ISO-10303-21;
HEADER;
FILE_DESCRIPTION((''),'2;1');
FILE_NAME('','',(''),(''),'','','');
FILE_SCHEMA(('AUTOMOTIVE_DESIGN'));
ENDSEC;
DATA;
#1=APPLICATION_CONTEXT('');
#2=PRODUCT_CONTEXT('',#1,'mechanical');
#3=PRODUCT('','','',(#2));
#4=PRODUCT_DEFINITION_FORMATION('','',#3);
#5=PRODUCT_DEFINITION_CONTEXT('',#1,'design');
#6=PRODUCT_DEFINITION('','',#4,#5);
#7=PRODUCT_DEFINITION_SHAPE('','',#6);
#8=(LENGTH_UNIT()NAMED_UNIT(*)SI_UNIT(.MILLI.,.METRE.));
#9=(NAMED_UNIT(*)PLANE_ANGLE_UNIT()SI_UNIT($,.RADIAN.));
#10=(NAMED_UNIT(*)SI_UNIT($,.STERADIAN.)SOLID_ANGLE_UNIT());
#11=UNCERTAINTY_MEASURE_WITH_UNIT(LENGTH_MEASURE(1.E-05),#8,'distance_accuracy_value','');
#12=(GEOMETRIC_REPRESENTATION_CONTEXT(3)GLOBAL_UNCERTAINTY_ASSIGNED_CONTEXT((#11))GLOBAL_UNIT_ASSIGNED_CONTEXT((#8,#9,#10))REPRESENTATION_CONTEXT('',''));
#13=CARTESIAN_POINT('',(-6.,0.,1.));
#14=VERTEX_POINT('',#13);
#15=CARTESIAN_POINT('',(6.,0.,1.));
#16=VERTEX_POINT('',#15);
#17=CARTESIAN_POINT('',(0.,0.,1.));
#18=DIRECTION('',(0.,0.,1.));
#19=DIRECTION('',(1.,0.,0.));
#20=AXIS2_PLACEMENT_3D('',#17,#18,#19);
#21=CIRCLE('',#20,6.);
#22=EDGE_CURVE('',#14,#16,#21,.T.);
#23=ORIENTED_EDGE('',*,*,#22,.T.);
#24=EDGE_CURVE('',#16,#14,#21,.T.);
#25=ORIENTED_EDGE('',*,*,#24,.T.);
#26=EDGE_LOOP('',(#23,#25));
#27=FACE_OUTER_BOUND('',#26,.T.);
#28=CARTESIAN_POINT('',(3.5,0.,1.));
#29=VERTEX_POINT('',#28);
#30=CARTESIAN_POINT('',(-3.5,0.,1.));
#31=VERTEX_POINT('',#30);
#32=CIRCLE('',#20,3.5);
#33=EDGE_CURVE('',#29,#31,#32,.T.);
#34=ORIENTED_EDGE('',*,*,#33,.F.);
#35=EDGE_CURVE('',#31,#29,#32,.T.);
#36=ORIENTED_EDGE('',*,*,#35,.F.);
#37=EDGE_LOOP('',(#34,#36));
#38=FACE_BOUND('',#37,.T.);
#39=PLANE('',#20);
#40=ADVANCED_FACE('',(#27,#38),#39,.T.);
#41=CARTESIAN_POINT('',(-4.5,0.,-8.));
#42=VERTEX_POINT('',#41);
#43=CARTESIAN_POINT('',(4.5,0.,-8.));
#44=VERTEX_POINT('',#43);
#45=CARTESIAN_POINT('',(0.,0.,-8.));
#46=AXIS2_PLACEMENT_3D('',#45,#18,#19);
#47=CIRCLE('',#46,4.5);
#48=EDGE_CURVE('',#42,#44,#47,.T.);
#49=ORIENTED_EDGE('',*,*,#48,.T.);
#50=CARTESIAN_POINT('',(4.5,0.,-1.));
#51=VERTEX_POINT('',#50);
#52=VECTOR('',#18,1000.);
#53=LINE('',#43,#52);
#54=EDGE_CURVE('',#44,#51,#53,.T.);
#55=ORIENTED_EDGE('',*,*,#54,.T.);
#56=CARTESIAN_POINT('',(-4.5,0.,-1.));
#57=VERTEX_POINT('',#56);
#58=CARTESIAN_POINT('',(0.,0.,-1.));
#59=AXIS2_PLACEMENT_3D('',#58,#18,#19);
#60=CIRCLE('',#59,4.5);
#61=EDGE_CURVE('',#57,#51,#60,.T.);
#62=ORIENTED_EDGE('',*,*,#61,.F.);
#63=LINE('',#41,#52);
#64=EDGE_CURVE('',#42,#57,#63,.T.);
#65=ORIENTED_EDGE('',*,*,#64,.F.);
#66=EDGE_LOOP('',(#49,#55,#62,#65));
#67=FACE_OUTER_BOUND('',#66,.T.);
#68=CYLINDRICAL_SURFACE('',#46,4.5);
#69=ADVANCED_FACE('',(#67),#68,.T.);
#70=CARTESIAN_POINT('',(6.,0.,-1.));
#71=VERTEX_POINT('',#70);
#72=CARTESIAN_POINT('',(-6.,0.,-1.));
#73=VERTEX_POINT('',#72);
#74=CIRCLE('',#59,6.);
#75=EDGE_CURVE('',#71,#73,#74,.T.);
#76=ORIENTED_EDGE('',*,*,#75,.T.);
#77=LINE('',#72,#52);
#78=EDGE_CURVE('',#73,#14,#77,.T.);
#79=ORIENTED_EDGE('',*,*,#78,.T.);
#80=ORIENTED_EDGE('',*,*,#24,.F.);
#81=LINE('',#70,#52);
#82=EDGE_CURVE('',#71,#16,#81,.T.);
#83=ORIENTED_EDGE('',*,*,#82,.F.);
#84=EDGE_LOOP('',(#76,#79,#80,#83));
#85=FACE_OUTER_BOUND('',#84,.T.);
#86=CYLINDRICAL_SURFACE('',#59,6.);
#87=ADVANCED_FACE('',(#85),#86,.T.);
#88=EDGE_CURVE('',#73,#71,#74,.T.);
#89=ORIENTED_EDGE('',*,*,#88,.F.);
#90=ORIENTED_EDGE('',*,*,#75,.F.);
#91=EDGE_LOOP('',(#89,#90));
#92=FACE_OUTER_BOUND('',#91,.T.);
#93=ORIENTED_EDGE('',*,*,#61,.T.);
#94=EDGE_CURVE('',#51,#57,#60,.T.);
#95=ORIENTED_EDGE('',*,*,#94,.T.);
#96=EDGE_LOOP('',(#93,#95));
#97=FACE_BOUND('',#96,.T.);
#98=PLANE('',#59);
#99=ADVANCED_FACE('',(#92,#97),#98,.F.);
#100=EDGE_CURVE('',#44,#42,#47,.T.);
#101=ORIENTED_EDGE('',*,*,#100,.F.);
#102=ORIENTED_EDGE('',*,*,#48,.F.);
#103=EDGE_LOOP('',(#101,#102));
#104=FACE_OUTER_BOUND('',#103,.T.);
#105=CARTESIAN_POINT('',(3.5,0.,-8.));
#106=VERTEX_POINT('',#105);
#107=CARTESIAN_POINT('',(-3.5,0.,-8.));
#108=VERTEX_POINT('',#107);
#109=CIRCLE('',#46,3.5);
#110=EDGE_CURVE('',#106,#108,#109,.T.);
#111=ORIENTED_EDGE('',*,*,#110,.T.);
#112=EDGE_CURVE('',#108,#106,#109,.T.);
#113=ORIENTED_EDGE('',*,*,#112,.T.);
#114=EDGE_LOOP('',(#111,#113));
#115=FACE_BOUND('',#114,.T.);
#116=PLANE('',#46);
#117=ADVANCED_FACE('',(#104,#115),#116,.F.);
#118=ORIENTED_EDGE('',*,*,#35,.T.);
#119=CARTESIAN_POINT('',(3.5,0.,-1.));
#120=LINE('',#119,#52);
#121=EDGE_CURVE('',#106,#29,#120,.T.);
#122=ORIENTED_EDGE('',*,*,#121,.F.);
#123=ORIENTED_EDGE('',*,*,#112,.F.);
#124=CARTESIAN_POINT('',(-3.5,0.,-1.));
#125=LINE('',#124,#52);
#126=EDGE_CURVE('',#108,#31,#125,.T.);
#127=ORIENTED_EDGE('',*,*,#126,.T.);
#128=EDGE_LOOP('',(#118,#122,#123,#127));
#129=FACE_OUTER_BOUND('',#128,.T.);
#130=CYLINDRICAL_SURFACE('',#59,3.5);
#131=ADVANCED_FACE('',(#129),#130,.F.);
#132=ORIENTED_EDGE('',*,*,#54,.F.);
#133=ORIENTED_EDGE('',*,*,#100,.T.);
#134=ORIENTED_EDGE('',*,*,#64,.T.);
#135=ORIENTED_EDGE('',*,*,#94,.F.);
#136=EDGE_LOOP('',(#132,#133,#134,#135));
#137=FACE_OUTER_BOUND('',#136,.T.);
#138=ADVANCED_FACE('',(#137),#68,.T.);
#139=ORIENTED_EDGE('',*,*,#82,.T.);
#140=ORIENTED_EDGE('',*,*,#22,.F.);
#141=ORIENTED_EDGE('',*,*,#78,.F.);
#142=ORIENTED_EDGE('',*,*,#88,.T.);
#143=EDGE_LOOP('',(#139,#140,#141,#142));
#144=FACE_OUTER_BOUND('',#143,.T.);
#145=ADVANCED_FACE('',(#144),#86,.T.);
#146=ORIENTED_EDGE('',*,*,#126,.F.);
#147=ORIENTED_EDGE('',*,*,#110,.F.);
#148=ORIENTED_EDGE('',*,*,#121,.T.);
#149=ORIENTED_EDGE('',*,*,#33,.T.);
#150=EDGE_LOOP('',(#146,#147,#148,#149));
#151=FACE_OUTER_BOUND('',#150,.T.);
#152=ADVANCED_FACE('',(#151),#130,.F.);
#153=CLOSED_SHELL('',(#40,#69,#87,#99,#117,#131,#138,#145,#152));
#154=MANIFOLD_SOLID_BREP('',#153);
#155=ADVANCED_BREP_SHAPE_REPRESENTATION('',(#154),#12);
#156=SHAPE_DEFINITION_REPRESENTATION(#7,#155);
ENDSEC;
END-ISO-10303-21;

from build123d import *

# Parameters (mm, degrees)
SKETCH_1_R      = 6
SKETCH_1_R_2    = 3.5
EXTRUDE_1_DEPTH = 1
EXTRUDE_START   = -8
SKETCH_2_R      = 4.5
SKETCH_2_R_2    = 3.5
EXTRUDE_2_DEPTH = 8


with BuildPart() as part:
    # 草图1 → 凸台-拉伸1 (new, symmetric)
    with BuildSketch(Plane.XY):
        Circle(SKETCH_1_R)
        Circle(SKETCH_1_R_2, mode=Mode.SUBTRACT)
    extrude(amount=EXTRUDE_1_DEPTH, both=True)

    # 草图2 → 凸台-拉伸2 (add)
    with BuildSketch(Plane.XY.offset(EXTRUDE_START)):
        Circle(SKETCH_2_R)
        Circle(SKETCH_2_R_2, mode=Mode.SUBTRACT)
    extrude(amount=EXTRUDE_2_DEPTH)


solid = part.part
